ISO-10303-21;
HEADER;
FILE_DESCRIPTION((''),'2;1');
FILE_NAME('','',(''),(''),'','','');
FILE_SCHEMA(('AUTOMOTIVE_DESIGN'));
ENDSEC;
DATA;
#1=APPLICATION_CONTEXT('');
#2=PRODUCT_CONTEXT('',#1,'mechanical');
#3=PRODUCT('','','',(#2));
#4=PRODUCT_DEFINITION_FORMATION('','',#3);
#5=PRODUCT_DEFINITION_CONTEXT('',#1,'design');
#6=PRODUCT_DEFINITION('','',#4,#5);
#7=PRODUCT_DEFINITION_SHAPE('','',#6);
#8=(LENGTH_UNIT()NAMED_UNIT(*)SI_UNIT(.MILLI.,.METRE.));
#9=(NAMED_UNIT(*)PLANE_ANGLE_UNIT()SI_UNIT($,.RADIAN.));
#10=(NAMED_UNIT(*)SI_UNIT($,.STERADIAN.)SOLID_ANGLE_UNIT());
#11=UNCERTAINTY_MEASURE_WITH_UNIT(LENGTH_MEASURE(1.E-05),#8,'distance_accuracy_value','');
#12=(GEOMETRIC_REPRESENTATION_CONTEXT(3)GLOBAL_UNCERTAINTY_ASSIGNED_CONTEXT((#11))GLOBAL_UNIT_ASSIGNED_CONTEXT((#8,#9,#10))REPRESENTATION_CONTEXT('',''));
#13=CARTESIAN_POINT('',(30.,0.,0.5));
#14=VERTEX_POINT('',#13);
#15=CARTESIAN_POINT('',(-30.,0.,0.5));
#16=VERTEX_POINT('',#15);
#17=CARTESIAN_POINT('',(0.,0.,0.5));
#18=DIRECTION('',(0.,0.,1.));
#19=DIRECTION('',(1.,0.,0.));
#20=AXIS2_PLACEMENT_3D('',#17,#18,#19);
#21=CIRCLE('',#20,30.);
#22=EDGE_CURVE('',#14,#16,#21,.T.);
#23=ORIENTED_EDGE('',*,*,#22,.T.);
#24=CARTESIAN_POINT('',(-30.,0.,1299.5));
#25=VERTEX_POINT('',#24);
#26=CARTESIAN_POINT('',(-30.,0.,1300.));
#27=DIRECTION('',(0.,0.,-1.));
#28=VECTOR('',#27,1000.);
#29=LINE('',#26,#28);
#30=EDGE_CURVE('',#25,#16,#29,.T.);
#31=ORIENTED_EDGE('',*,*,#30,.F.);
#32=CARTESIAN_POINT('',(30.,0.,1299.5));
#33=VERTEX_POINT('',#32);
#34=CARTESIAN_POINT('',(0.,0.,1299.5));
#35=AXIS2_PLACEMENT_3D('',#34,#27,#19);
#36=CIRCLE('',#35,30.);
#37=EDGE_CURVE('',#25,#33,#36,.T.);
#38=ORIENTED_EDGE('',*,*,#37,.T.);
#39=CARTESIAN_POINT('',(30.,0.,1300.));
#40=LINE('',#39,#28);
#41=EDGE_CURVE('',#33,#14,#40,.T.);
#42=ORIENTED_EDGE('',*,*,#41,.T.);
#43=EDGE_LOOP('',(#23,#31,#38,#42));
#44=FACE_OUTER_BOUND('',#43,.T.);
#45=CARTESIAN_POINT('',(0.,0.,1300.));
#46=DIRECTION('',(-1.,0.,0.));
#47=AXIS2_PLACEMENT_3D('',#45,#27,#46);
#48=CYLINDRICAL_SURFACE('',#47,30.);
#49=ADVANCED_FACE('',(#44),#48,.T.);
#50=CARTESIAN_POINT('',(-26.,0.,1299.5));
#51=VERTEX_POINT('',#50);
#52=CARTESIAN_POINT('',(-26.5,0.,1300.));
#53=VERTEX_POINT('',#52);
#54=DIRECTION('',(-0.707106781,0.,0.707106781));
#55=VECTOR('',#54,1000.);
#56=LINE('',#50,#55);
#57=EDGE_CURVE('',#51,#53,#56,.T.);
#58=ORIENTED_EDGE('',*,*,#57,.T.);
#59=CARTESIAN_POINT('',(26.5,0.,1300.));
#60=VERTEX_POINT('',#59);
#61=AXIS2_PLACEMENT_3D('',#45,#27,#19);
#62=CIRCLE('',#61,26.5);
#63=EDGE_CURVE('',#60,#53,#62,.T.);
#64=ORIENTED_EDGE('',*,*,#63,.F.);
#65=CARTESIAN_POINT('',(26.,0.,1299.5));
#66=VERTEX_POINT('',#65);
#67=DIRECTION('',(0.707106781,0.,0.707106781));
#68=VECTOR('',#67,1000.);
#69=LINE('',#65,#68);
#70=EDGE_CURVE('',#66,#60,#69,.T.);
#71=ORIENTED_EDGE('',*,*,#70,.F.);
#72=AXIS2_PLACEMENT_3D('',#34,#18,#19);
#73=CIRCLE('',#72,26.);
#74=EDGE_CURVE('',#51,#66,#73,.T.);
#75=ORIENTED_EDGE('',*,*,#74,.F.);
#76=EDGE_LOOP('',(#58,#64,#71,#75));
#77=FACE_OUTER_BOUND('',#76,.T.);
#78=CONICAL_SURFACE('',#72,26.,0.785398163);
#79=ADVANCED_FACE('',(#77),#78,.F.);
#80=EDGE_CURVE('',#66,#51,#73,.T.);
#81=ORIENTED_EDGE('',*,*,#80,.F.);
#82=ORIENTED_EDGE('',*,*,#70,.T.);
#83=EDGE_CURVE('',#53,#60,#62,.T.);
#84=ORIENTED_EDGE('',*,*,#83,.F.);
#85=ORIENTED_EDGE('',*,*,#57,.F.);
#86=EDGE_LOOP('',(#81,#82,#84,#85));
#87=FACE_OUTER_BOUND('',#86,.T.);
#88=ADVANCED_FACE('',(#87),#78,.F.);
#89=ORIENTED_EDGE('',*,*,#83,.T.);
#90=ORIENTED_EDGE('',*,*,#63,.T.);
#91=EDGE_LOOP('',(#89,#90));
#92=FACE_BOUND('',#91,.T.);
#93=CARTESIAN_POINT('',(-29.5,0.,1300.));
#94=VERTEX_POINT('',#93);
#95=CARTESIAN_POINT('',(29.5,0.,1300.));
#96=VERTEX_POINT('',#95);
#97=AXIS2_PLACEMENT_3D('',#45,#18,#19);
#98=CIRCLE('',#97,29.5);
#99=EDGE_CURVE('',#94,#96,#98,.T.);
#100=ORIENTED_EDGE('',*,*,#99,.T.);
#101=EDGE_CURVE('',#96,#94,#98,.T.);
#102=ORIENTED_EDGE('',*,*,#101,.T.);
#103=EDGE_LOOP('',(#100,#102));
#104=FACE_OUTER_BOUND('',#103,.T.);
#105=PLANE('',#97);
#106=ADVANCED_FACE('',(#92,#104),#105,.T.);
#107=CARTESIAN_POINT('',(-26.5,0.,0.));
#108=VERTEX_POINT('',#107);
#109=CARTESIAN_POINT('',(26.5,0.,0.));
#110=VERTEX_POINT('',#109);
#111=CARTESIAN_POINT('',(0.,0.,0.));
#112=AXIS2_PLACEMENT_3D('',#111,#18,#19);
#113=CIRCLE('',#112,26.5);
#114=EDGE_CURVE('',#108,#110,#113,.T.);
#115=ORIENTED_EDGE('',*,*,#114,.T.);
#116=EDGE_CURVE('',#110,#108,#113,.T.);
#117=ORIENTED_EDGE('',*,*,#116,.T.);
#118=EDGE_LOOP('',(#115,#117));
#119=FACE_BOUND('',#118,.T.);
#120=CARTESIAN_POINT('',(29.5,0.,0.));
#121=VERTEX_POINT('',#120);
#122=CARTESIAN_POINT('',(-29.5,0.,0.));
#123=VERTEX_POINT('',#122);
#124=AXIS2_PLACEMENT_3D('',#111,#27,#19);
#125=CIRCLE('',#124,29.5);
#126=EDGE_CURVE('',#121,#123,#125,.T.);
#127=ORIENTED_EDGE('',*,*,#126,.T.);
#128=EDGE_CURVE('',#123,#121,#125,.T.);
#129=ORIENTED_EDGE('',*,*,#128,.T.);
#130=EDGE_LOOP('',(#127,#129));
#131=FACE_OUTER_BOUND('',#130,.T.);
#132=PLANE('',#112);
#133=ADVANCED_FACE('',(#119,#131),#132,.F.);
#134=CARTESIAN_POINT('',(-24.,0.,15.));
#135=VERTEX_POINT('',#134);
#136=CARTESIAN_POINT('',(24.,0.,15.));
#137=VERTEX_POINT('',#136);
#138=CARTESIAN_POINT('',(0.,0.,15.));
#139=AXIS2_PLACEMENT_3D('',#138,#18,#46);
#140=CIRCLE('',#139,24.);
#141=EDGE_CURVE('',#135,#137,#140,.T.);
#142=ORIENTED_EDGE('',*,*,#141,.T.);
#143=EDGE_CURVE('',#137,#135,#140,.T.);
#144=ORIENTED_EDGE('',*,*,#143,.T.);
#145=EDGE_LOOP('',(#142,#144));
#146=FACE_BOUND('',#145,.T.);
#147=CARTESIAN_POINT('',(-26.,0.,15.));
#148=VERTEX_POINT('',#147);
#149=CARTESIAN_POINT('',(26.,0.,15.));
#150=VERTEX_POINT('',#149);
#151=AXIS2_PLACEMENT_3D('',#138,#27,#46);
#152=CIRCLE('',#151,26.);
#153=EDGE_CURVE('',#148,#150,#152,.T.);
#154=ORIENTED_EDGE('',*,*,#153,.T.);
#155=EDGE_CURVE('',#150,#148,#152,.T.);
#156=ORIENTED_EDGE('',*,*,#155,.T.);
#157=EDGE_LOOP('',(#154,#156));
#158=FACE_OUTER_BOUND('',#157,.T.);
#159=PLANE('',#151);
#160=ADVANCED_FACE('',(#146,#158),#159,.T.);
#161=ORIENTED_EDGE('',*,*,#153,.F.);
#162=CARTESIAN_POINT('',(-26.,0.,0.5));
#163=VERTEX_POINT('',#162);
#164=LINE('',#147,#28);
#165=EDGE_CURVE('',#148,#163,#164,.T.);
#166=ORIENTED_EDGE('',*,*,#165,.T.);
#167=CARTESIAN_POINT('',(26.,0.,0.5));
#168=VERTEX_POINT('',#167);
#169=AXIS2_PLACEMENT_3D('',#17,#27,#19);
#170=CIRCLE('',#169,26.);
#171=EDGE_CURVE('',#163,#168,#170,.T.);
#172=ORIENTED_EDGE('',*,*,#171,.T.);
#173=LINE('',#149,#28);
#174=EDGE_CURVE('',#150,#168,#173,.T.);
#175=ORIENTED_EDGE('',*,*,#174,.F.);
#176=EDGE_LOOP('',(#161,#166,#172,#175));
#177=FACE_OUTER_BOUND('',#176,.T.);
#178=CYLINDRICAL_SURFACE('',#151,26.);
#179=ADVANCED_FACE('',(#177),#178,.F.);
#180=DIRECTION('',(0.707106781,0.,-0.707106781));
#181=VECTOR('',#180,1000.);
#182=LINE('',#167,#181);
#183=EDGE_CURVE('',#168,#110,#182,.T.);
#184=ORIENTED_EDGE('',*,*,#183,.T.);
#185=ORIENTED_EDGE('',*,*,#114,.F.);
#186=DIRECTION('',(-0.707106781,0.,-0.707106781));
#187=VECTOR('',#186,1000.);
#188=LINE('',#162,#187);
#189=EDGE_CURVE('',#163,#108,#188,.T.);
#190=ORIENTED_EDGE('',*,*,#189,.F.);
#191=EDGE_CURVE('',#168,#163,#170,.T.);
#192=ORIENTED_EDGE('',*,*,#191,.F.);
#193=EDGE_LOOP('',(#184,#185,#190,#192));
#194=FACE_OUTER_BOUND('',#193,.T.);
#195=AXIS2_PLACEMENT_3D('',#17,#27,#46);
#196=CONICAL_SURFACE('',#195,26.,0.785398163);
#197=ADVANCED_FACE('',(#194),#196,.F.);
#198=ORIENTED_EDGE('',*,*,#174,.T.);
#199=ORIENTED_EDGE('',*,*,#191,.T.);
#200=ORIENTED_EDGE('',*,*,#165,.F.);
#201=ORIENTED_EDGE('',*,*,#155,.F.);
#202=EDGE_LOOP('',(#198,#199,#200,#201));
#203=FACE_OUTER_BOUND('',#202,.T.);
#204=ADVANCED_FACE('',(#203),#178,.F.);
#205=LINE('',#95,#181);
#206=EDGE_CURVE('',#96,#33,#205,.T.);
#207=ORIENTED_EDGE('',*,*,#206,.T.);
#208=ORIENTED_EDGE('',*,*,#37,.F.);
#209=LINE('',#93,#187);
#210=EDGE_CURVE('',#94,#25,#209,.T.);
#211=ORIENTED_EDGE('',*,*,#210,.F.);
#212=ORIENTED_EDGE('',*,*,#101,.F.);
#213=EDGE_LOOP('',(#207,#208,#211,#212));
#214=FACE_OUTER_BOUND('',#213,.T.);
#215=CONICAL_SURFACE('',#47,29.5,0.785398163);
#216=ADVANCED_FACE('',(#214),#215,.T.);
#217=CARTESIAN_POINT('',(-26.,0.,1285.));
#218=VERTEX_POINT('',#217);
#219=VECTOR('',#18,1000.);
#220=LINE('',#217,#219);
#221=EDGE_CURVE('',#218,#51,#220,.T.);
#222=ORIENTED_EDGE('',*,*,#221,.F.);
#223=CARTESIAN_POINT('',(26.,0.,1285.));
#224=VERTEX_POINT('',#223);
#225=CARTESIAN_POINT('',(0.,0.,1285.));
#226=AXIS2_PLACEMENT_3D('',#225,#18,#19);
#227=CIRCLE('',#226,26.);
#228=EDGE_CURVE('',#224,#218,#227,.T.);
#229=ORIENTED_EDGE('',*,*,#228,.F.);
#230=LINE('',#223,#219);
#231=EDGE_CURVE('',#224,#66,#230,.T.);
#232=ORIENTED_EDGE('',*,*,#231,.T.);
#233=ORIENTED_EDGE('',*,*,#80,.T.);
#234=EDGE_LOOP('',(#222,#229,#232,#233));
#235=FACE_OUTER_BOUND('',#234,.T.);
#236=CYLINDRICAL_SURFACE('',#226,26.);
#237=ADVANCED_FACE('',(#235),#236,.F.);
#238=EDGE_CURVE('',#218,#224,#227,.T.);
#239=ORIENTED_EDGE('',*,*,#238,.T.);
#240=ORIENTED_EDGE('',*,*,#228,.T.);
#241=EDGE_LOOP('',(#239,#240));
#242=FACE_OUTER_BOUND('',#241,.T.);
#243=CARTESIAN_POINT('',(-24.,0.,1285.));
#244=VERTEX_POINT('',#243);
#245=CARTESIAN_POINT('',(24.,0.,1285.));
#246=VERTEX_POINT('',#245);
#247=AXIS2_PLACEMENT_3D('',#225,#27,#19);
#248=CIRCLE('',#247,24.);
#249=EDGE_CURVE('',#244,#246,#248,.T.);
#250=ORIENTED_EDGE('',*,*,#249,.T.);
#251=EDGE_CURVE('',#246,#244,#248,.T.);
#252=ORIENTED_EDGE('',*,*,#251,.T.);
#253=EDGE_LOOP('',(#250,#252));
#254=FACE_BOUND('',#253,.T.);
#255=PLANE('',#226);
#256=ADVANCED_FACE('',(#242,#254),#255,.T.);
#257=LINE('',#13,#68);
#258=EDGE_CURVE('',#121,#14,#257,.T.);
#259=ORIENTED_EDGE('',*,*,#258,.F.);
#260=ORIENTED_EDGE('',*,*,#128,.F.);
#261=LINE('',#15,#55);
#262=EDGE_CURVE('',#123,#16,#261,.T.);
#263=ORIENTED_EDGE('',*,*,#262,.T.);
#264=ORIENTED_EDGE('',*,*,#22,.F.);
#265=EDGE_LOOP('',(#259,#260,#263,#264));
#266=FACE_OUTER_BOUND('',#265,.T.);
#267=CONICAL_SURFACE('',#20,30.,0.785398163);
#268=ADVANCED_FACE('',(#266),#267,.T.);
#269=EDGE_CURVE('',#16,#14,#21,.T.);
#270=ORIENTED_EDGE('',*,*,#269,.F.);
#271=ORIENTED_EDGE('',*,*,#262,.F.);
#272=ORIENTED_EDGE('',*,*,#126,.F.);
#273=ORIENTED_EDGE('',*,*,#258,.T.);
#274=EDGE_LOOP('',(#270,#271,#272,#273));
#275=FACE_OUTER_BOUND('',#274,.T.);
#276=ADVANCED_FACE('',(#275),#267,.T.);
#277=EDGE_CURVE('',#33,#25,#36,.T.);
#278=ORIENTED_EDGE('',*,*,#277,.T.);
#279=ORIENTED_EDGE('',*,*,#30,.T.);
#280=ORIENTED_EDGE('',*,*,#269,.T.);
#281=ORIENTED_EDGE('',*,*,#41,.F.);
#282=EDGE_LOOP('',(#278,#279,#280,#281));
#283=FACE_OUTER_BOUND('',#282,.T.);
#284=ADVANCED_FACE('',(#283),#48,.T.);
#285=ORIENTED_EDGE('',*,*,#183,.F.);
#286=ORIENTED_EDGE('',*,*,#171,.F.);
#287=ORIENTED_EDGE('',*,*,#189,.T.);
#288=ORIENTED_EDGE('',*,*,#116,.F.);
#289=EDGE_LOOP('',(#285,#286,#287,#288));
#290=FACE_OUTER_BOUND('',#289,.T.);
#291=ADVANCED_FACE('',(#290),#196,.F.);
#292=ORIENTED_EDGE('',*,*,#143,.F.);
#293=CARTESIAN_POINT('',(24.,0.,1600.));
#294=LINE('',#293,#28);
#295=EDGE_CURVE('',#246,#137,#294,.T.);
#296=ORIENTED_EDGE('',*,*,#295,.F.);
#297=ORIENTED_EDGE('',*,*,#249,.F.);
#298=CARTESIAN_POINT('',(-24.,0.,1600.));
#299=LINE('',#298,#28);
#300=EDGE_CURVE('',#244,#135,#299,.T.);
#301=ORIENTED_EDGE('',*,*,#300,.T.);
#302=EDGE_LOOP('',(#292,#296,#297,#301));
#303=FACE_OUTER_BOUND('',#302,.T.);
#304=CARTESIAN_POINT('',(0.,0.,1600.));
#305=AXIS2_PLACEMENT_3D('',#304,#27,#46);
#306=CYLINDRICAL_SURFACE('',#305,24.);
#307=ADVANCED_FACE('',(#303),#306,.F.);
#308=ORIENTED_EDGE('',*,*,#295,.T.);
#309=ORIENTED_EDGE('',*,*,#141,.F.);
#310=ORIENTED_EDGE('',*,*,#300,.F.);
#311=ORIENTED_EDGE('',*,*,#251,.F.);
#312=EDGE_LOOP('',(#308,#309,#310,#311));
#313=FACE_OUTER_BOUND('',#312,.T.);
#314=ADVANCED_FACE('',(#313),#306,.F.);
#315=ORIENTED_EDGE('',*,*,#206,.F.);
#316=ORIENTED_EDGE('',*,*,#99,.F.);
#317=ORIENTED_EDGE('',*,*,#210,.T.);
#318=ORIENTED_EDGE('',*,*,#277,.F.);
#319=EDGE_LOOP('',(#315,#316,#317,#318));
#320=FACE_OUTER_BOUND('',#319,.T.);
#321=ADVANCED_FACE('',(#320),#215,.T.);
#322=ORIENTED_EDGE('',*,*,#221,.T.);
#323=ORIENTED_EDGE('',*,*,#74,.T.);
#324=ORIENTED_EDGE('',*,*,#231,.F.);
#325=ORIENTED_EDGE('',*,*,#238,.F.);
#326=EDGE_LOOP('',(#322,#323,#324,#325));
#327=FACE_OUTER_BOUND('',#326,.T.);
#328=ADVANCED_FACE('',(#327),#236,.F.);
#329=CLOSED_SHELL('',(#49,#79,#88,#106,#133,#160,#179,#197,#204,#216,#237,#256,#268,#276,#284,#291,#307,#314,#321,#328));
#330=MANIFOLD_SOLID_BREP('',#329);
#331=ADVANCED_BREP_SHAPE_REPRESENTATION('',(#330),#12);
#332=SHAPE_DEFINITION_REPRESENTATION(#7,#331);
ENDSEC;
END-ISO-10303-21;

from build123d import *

# Parameters (mm, degrees)
SKETCH_1_R          = 30
EXTRUDE_1_DEPTH     = 1300
SKETCH_2_R          = 24
CUT_EXTRUDE_1_DEPTH = 1600
SKETCH_3_R          = 26
CUT_EXTRUDE_2_DEPTH = 15
CUT_EXTRUDE_START   = -15
SKETCH_4_R          = 26
CUT_EXTRUDE_3_DEPTH = 15
CHAMFER_1_SIZE      = 0.5


with BuildPart() as part:
    # 草图1 → 凸台-拉伸1 (new body)
    with BuildSketch(Plane.XY):
        Circle(SKETCH_1_R)
    extrude(amount=EXTRUDE_1_DEPTH)

    # 草图2 → 切除-拉伸1 (cut)
    with BuildSketch(Plane(origin=(0, 0, 0), x_dir=(-1, 0, 0), z_dir=(0, 0, -1))):
        Circle(SKETCH_2_R)
    extrude(amount=-CUT_EXTRUDE_1_DEPTH, mode=Mode.SUBTRACT)

    # 草图3 → 切除-拉伸2 (cut)
    with BuildSketch(Plane(origin=(0, 0, 0), x_dir=(-1, 0, 0), z_dir=(0, 0, -1))):
        Circle(SKETCH_3_R)
    extrude(amount=-CUT_EXTRUDE_2_DEPTH, mode=Mode.SUBTRACT)

    # 草图4 → 切除-拉伸3 (cut)
    with BuildSketch(Plane.XY.offset(1300).offset(CUT_EXTRUDE_START)):
        with Locations(Location((0, 0, 0), (0, 0, 180))):
            Circle(SKETCH_4_R)
    extrude(amount=CUT_EXTRUDE_3_DEPTH, mode=Mode.SUBTRACT)

    # 倒角1
    chamfer_1_edges = [part.edges().sort_by_distance(p)[0] for p in [
        (26, 0, 0),
        (-30, 0, 0),
        (26, 0, 1300),
        (-30, 0, 1300),
    ]]
    chamfer(chamfer_1_edges, length=CHAMFER_1_SIZE)


solid = part.part
